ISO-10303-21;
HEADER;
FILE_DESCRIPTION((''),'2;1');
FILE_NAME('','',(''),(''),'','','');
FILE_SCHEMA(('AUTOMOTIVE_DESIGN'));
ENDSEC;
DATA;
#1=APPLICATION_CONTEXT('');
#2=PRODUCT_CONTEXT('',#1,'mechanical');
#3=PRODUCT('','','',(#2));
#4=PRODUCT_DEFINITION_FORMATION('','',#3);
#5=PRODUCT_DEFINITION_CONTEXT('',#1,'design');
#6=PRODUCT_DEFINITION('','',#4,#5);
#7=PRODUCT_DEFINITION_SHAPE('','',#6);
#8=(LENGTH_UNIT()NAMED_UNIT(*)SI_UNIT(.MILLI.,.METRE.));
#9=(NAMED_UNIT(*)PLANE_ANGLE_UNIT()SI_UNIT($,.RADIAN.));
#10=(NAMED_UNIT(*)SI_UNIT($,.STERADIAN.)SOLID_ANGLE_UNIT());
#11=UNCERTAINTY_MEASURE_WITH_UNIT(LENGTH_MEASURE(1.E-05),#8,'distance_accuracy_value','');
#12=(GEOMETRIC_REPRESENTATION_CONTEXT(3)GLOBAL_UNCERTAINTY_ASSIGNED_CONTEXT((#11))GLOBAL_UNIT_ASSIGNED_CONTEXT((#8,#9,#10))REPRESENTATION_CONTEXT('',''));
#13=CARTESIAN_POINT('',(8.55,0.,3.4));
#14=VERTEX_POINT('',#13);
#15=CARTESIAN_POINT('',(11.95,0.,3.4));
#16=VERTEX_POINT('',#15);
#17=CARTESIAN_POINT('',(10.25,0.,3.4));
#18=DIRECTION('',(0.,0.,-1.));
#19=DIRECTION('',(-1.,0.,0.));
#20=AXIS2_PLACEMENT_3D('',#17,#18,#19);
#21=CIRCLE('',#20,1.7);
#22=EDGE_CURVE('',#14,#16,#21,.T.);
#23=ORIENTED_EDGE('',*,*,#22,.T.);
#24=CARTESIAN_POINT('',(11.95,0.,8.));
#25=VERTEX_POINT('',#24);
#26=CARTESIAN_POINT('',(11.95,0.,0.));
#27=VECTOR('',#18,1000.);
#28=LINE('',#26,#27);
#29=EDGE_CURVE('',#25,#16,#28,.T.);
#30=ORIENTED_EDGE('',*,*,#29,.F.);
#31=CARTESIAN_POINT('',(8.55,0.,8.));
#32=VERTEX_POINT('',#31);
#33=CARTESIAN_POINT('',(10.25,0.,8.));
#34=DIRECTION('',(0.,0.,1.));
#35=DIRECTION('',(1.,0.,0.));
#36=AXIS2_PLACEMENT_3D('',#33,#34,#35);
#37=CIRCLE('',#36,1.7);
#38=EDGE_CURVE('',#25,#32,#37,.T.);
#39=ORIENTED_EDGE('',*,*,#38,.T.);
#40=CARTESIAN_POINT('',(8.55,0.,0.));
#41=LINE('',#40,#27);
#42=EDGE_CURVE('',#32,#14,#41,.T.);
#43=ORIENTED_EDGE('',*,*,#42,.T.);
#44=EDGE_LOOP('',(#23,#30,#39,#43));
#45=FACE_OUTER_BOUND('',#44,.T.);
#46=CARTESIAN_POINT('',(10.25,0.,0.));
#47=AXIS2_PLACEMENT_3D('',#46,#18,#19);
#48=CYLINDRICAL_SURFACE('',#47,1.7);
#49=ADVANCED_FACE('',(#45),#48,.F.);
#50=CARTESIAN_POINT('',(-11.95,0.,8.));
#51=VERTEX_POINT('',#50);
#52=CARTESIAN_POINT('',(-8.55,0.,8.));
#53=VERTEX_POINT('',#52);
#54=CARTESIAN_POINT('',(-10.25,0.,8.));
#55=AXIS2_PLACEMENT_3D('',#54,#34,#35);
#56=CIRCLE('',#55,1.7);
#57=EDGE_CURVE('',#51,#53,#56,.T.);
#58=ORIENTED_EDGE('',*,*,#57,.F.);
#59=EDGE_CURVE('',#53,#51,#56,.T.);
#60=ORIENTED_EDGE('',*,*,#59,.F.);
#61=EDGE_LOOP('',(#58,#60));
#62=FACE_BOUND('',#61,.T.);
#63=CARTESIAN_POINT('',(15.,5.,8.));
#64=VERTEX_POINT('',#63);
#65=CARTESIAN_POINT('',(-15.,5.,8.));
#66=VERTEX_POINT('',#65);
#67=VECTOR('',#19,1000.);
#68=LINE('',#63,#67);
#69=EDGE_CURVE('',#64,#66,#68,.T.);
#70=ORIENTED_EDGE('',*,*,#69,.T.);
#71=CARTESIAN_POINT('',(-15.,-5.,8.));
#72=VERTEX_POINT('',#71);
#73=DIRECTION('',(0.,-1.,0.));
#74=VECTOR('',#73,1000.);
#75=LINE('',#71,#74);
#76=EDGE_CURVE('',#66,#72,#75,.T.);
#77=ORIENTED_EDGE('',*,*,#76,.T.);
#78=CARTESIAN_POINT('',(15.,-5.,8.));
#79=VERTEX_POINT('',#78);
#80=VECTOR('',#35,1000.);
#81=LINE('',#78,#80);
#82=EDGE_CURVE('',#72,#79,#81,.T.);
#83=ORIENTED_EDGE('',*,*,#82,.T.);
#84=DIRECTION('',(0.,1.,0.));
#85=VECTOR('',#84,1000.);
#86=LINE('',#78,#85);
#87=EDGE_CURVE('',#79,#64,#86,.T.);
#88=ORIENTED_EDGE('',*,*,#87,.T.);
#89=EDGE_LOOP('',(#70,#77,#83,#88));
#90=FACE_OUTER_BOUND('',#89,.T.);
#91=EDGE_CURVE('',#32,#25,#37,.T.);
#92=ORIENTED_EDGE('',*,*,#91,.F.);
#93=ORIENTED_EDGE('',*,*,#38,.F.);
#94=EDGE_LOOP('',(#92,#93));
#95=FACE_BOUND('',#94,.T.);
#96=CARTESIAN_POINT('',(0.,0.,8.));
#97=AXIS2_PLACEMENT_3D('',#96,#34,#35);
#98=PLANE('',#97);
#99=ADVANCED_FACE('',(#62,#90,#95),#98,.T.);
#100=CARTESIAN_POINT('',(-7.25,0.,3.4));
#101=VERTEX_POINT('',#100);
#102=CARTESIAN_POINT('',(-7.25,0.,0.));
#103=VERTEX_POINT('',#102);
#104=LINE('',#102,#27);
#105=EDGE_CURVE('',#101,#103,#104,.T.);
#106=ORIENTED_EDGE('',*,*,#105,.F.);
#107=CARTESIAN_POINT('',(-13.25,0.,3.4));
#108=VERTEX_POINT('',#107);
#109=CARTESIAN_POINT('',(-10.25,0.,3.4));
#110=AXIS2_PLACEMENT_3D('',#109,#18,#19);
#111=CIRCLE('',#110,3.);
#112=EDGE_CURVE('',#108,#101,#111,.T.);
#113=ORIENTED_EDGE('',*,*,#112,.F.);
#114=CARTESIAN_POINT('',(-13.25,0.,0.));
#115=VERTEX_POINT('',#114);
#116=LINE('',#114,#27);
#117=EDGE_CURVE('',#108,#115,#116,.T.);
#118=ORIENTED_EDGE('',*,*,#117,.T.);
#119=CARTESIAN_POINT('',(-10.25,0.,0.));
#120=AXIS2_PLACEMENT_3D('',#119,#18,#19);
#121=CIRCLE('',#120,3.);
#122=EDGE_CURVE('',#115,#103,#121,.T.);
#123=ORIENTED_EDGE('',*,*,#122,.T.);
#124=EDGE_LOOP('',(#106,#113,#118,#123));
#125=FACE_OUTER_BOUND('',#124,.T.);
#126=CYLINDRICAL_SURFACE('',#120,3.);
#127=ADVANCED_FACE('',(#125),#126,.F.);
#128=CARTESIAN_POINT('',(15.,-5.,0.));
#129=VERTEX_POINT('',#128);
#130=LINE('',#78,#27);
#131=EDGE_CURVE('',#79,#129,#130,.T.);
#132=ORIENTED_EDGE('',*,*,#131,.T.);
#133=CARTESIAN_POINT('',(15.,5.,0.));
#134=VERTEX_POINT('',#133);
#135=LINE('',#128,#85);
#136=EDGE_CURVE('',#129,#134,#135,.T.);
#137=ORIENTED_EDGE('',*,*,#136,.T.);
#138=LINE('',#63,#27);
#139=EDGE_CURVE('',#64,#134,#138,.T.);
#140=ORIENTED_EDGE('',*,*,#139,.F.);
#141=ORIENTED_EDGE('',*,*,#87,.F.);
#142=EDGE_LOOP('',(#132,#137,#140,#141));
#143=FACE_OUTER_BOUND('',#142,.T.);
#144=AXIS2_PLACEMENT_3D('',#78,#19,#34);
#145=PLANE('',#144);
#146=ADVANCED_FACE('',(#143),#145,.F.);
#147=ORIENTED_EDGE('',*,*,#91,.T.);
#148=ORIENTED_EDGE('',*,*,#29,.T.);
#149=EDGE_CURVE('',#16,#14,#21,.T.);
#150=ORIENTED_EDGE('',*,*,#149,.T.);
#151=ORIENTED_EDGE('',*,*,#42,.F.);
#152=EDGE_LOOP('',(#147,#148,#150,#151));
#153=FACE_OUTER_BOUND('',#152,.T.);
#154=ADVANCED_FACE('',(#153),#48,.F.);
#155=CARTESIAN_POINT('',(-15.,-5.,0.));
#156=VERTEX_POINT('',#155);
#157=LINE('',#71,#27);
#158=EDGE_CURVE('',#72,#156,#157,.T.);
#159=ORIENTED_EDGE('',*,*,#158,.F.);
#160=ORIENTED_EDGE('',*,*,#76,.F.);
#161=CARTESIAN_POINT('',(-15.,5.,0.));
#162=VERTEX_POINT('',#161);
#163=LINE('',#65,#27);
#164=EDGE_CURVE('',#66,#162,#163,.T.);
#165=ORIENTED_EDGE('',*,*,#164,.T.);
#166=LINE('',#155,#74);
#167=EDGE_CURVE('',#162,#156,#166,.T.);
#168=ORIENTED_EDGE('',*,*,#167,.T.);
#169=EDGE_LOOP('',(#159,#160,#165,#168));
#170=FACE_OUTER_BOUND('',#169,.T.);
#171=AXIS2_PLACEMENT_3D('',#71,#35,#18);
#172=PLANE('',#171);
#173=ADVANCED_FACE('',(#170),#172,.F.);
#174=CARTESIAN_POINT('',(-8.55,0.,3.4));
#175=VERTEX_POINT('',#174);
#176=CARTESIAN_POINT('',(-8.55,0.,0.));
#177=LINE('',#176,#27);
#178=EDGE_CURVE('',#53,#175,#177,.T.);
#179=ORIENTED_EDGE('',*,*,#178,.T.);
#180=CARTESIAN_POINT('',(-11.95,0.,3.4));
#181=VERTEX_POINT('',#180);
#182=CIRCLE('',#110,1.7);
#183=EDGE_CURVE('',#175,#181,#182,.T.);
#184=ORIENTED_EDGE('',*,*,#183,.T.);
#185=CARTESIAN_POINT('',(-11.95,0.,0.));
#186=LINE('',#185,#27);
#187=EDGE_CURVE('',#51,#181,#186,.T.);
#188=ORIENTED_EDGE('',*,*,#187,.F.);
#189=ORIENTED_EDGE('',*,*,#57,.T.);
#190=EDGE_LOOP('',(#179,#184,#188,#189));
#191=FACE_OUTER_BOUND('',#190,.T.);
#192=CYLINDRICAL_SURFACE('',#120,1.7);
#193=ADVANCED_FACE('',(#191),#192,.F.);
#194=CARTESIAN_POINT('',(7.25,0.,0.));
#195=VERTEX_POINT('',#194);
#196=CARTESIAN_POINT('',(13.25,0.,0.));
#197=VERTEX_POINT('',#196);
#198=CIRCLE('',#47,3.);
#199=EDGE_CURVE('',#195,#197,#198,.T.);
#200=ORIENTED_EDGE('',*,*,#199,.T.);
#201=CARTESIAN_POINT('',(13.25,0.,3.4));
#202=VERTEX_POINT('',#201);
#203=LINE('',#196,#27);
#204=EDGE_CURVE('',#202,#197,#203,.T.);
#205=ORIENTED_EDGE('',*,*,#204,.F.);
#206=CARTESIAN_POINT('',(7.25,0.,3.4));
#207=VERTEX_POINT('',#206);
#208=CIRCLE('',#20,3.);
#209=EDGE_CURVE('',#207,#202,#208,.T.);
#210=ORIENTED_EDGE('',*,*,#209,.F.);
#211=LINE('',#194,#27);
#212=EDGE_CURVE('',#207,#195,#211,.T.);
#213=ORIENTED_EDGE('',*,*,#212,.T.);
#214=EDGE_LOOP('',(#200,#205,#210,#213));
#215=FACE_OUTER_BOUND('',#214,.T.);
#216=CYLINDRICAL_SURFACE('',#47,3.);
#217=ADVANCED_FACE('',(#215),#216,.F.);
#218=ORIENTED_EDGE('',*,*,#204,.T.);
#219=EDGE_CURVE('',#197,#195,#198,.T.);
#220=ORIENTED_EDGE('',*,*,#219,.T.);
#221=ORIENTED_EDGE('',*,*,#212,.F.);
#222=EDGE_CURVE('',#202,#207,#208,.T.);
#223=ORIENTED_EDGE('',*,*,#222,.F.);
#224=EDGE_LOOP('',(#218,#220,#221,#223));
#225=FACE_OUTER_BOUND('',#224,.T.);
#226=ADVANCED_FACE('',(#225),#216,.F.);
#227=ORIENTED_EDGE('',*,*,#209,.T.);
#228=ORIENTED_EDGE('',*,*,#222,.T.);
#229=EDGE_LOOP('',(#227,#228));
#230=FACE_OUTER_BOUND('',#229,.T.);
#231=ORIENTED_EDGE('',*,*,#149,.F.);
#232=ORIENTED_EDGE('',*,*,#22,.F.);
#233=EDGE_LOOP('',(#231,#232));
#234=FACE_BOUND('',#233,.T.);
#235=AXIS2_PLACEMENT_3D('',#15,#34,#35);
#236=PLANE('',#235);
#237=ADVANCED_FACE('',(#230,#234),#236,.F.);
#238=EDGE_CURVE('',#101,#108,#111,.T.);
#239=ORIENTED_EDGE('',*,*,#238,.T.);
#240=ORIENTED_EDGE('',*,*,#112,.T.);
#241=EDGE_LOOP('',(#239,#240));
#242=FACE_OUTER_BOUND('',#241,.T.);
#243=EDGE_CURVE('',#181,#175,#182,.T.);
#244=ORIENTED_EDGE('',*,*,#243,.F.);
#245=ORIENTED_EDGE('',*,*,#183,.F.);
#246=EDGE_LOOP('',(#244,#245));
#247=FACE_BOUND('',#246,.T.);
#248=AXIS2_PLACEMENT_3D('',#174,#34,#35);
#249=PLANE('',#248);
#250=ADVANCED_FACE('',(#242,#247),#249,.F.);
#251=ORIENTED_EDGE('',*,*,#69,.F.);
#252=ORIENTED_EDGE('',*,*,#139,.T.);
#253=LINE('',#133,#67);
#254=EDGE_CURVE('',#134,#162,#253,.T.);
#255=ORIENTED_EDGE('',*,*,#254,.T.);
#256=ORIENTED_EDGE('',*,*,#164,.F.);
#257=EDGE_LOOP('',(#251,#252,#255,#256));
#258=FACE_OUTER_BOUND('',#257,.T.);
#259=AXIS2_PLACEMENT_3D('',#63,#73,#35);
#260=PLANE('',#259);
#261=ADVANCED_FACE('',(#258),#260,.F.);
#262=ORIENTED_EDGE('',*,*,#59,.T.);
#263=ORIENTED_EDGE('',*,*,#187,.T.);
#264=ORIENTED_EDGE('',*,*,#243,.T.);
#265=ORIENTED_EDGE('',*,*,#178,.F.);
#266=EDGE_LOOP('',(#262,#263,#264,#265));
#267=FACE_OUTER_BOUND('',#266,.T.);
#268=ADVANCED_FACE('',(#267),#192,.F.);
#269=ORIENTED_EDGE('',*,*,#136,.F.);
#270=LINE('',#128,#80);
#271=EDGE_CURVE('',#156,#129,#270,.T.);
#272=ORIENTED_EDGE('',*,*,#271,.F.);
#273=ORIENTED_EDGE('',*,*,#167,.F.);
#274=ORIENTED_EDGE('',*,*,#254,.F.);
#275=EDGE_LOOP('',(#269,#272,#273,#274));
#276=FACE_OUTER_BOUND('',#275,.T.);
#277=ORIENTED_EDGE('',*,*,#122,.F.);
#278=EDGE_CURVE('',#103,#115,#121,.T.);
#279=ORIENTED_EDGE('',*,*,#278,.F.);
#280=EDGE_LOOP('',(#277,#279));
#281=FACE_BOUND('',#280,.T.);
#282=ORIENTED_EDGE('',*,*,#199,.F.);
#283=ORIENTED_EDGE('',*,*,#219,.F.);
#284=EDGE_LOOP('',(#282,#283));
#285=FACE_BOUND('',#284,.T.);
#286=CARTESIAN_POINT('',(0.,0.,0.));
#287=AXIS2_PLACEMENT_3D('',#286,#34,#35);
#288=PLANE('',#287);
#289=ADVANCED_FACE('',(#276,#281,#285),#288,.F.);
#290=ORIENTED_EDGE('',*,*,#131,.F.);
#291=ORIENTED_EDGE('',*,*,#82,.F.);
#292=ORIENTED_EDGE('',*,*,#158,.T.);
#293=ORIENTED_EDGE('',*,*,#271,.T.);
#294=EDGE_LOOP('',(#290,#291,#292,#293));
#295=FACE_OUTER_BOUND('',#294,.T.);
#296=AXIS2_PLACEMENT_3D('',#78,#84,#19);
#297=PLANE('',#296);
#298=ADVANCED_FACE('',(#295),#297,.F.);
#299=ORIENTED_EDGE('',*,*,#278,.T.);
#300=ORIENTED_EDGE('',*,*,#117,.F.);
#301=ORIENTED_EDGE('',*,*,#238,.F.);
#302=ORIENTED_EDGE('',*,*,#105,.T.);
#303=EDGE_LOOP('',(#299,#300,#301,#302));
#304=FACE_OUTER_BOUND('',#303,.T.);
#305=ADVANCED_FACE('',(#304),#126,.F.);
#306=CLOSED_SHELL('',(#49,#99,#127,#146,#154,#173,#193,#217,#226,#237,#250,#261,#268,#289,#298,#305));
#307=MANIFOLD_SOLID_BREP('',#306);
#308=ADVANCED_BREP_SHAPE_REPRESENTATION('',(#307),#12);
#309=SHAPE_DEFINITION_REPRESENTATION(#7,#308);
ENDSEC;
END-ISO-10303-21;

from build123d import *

# Parameters (mm, degrees)
SKETCH_1_W                = 30
SKETCH_1_H                = 10
EXTRUDE_1_DEPTH           = 8
HOLE_WIZARD_1_D           = 3.4
HOLE_WIZARD_1_CBORE_D     = 6
HOLE_WIZARD_1_CBORE_DEPTH = 3.4


with BuildPart() as part:
    # 草图1 → 凸台-拉伸1 (new body)
    with BuildSketch(Plane.XY):
        Rectangle(SKETCH_1_W, SKETCH_1_H)
    extrude(amount=EXTRUDE_1_DEPTH)

    # 打孔尺寸(%根据)内六角圆柱头螺钉的类型1 (through all)
    with Locations(Plane(origin=(0, 0, 0), x_dir=(-1, 0, 0), z_dir=(0, 0, -1))):
        with Locations((-10.25, 0), (10.25, 0)):
            CounterBoreHole(HOLE_WIZARD_1_D / 2, HOLE_WIZARD_1_CBORE_D / 2, HOLE_WIZARD_1_CBORE_DEPTH)


solid = part.part
